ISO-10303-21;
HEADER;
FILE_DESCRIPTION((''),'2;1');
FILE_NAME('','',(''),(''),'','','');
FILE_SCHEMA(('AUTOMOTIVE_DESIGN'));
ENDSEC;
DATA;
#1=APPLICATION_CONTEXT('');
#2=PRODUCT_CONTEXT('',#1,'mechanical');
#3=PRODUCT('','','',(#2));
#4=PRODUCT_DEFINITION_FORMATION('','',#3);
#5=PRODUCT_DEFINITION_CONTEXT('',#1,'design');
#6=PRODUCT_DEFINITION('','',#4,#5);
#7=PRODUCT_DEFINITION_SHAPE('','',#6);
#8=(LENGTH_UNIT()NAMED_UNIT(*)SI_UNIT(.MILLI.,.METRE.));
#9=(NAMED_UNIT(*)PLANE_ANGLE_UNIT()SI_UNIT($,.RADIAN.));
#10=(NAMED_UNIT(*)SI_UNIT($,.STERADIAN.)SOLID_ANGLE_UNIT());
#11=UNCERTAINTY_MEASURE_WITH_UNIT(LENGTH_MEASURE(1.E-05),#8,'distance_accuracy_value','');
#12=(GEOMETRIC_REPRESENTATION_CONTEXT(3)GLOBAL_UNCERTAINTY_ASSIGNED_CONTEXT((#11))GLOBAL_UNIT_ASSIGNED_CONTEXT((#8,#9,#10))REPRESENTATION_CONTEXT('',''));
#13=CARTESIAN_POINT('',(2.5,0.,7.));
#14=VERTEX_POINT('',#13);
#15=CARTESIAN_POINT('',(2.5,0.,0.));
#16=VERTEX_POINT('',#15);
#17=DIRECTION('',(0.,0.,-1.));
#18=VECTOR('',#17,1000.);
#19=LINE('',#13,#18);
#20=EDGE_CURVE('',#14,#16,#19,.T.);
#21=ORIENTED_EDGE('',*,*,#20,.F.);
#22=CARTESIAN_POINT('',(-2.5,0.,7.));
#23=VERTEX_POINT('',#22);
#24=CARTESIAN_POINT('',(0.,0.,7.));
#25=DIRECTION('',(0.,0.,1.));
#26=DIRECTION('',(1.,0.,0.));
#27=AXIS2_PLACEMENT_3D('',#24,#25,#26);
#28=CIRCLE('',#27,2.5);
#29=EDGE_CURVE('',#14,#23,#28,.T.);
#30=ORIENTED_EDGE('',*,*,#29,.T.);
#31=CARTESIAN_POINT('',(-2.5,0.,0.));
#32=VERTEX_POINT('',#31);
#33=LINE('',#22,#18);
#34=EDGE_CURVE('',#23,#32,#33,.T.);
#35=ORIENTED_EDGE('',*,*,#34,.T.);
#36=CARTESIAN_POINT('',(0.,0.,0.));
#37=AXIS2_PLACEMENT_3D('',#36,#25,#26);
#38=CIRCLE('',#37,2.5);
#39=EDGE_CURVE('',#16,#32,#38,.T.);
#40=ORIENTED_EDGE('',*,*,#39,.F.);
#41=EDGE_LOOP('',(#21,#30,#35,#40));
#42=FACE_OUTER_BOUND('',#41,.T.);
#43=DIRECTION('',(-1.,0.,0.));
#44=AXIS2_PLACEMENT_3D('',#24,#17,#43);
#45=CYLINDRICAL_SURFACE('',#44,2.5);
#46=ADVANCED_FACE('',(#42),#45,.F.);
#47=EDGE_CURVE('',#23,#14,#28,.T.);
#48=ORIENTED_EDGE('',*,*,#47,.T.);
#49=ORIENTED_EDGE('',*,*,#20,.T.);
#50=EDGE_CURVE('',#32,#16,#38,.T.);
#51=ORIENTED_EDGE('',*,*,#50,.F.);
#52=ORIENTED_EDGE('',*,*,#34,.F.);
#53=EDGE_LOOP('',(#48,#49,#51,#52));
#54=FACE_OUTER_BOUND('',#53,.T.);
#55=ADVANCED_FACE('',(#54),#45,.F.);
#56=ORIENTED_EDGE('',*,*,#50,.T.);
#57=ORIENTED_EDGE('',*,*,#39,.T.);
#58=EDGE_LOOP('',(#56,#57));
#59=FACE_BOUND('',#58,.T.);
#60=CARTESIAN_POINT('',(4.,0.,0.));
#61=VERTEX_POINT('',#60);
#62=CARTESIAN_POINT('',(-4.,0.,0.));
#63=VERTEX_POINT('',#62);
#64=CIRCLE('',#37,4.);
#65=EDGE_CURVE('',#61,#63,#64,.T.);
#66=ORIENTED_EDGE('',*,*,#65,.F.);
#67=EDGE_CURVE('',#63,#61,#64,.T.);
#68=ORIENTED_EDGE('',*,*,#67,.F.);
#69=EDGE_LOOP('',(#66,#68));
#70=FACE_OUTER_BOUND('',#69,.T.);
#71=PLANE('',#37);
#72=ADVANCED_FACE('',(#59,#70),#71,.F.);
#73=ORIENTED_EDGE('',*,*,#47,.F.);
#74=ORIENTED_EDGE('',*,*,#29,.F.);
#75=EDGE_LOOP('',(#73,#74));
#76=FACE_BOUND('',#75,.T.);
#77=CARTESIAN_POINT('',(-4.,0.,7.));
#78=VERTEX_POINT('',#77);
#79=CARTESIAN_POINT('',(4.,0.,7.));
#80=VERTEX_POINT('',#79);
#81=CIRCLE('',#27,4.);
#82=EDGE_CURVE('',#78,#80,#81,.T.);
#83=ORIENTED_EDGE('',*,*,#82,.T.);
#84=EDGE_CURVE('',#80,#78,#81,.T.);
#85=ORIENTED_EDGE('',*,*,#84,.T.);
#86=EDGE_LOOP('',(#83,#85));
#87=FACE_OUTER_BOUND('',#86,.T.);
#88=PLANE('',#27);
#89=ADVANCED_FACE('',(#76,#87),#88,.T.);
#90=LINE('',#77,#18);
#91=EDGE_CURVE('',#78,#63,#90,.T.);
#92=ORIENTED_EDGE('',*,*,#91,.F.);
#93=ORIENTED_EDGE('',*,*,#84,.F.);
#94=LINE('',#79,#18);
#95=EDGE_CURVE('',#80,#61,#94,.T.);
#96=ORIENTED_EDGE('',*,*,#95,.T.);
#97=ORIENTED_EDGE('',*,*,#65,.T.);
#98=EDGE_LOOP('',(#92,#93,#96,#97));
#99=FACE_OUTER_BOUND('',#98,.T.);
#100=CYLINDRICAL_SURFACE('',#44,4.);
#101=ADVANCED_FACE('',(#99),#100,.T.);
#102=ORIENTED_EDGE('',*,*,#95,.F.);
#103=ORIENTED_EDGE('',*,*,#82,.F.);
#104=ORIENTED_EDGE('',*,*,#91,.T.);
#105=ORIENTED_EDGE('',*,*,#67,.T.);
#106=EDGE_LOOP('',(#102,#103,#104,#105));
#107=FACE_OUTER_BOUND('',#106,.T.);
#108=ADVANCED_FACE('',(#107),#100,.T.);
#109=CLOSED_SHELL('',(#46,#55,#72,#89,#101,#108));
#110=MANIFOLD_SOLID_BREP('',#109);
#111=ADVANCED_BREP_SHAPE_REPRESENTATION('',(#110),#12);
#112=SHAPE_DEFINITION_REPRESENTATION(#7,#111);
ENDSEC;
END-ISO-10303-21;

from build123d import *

# Parameters (mm, degrees)
SKETCH_1_R      = 4
SKETCH_1_R_2    = 2.5
EXTRUDE_1_DEPTH = 7


with BuildPart() as part:
    # 草图1 → 凸台-拉伸1 (new body)
    with BuildSketch(Plane.XY):
        Circle(SKETCH_1_R)
        Circle(SKETCH_1_R_2, mode=Mode.SUBTRACT)
    extrude(amount=EXTRUDE_1_DEPTH)


solid = part.part
